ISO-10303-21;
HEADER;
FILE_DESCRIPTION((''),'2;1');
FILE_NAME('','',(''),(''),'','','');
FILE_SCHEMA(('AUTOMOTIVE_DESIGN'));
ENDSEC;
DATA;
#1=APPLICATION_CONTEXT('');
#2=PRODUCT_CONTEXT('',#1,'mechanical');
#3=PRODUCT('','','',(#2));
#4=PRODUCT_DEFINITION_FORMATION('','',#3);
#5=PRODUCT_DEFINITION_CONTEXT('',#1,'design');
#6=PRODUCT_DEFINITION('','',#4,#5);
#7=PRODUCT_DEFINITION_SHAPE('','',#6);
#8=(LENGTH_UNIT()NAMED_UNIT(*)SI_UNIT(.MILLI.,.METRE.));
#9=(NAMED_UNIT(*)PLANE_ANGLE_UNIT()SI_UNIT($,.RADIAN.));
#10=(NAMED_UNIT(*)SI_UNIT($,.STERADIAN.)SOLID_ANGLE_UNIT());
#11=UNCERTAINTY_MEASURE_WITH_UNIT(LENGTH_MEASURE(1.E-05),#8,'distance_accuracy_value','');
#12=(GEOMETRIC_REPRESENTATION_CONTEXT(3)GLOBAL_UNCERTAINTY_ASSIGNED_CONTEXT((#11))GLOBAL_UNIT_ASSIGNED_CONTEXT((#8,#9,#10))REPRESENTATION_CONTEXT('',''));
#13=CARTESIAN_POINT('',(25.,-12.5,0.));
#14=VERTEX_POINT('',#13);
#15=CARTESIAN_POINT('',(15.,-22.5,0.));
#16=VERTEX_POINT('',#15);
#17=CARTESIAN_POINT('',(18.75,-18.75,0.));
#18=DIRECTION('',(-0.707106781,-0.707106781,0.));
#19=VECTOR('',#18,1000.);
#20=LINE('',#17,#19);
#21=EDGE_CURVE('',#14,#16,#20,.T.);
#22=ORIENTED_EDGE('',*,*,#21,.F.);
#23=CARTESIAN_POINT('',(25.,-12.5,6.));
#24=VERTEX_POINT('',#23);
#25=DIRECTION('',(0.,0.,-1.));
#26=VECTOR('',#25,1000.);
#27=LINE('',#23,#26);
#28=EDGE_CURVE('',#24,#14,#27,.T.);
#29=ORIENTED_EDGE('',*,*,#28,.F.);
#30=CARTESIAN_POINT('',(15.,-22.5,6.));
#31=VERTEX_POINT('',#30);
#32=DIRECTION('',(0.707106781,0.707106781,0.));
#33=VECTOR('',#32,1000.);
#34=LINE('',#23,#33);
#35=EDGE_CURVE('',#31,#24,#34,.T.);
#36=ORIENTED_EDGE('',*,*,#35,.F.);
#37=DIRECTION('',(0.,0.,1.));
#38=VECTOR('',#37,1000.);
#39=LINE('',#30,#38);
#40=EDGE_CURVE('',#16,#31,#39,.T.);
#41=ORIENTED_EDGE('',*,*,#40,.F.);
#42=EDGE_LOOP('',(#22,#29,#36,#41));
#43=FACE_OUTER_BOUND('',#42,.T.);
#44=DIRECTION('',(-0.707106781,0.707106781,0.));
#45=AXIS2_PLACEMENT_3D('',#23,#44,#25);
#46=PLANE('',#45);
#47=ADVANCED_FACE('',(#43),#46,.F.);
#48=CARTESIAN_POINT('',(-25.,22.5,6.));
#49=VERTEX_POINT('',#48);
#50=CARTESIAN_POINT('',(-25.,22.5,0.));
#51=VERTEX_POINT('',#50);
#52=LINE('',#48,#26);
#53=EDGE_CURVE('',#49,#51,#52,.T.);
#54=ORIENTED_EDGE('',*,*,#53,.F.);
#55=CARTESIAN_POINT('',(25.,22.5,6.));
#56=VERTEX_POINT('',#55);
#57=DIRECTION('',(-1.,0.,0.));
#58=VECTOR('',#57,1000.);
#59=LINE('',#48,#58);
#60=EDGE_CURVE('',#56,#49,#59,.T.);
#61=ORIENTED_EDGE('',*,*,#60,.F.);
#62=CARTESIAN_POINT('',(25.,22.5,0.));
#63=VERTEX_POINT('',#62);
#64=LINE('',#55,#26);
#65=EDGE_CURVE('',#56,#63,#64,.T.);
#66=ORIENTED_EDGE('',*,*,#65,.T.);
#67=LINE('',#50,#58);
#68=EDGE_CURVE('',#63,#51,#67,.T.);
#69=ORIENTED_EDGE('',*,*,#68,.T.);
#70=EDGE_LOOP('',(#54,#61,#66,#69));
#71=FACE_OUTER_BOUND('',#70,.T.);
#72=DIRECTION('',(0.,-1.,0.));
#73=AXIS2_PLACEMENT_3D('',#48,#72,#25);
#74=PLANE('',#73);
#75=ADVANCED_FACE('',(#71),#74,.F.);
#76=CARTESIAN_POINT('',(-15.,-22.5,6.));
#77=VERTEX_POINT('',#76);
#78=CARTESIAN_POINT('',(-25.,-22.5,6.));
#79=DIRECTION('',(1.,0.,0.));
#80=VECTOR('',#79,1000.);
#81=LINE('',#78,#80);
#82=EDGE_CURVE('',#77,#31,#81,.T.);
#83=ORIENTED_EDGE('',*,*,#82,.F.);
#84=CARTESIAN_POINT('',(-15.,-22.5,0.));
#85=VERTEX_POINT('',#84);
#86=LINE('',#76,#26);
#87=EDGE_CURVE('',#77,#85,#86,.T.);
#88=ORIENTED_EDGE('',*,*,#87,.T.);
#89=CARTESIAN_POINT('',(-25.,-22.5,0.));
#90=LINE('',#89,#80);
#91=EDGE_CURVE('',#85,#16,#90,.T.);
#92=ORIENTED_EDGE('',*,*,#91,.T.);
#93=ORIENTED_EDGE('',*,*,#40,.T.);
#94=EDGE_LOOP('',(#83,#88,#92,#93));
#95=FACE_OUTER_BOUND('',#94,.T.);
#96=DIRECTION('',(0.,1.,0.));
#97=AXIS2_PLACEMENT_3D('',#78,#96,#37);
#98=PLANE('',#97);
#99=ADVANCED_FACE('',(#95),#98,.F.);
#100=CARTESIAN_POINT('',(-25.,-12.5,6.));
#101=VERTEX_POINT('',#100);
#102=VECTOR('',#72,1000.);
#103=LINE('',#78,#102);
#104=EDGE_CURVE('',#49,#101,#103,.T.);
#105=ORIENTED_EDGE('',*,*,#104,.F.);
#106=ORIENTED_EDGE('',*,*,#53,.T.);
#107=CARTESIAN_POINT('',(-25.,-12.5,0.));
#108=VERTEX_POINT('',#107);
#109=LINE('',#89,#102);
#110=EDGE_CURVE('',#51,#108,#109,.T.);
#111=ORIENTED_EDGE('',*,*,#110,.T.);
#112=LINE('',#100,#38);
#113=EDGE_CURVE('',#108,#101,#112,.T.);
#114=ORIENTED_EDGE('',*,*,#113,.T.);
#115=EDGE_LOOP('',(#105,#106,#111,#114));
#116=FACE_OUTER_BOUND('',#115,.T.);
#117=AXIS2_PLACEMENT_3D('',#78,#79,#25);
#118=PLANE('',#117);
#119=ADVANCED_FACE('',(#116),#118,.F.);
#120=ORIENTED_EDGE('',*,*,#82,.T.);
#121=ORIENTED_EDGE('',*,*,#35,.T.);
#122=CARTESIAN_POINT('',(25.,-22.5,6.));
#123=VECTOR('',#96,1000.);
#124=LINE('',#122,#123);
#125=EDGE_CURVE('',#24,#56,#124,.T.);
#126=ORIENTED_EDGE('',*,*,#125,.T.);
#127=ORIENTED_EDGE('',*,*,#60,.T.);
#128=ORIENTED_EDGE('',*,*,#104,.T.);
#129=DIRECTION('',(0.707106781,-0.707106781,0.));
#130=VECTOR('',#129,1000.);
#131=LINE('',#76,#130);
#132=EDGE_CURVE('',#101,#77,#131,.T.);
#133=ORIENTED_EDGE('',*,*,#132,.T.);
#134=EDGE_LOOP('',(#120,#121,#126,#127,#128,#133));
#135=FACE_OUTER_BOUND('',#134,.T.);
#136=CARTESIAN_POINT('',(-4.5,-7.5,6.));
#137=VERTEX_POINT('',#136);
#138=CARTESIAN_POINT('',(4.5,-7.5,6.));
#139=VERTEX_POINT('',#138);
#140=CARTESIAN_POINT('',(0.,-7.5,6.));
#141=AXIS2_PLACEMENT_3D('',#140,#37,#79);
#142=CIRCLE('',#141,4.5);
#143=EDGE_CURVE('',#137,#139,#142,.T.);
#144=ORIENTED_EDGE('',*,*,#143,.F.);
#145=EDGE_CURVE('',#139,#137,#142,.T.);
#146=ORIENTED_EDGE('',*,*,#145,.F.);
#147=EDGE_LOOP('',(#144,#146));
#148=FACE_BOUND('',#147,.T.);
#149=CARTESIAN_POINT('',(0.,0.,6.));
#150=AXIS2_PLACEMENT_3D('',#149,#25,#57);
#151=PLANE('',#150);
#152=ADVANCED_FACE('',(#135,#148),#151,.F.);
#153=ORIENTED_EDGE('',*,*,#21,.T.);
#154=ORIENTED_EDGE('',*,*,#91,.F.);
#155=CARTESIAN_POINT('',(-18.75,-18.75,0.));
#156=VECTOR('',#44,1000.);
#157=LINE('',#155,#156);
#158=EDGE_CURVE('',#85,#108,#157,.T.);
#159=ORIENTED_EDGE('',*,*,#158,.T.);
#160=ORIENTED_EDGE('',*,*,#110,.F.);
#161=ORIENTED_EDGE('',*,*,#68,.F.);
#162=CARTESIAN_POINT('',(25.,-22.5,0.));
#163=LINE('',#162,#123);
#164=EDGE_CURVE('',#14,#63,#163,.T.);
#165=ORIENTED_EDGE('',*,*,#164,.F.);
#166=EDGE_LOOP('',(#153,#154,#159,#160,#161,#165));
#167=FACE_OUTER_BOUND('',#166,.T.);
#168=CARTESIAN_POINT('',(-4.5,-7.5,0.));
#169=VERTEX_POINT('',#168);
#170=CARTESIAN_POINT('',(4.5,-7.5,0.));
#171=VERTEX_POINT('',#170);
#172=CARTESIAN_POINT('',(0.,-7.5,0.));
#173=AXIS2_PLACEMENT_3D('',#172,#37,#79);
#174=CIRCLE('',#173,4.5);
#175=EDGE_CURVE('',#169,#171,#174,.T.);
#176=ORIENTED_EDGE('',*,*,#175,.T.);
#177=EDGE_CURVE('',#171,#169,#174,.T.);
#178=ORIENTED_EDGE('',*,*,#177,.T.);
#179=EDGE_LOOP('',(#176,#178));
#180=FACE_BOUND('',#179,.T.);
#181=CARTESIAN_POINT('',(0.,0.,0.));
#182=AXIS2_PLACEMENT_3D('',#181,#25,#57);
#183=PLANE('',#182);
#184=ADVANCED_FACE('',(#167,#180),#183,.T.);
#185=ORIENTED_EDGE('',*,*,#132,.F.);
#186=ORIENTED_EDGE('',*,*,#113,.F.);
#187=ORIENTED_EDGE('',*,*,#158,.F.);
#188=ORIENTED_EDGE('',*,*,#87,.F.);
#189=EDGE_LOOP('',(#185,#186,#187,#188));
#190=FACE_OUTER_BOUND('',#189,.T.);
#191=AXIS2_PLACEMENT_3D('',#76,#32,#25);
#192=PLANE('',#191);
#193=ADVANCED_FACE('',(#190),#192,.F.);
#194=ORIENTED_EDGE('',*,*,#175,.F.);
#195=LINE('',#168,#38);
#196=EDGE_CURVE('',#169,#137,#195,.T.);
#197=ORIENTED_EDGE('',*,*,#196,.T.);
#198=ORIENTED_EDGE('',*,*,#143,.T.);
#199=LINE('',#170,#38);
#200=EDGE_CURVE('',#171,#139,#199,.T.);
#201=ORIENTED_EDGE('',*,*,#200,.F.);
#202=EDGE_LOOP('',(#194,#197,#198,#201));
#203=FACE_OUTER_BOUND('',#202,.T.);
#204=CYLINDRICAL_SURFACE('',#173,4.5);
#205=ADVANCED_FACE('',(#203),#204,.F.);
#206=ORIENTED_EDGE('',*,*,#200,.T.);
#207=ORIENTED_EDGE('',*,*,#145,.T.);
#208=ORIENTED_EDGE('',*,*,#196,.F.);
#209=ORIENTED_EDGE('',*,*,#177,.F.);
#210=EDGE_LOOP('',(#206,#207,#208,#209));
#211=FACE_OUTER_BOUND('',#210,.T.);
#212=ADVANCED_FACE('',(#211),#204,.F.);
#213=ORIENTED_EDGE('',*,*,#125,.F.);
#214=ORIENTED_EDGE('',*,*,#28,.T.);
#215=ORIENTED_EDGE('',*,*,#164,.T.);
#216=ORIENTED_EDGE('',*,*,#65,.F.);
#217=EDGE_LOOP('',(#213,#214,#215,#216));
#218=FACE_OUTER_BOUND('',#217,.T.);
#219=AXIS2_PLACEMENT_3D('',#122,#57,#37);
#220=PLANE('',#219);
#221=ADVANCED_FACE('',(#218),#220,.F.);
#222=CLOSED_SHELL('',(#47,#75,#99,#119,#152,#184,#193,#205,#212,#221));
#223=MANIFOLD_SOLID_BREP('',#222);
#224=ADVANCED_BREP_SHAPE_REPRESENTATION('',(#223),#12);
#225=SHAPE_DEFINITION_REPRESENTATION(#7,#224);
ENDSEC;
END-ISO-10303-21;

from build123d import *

# Parameters (mm, degrees)
SKETCH1_W           = 50
SKETCH1_H           = 45
BOSS_EXTRUDE1_DEPTH = 6
SKETCH2_R           = 4.5
CUT_EXTRUDE1_DEPTH  = 6
CHAMFER1_SIZE       = 10


with BuildPart() as part:
    # Sketch1 → Boss-Extrude1 (new body)
    with BuildSketch(Plane.XY):
        Rectangle(SKETCH1_W, SKETCH1_H)
    extrude(amount=BOSS_EXTRUDE1_DEPTH)

    # Sketch2 → Cut-Extrude1 (cut)
    with BuildSketch(Plane.XY.offset(6)):
        with Locations((0, -7.5)):
            Circle(SKETCH2_R)
    extrude(amount=-CUT_EXTRUDE1_DEPTH, mode=Mode.SUBTRACT)

    # Chamfer1
    chamfer1_edges = [part.edges().sort_by_distance(p)[0] for p in [
        (25, -22.5, 3),
        (-25, -22.5, 3),
    ]]
    chamfer(chamfer1_edges, length=CHAMFER1_SIZE)


solid = part.part
